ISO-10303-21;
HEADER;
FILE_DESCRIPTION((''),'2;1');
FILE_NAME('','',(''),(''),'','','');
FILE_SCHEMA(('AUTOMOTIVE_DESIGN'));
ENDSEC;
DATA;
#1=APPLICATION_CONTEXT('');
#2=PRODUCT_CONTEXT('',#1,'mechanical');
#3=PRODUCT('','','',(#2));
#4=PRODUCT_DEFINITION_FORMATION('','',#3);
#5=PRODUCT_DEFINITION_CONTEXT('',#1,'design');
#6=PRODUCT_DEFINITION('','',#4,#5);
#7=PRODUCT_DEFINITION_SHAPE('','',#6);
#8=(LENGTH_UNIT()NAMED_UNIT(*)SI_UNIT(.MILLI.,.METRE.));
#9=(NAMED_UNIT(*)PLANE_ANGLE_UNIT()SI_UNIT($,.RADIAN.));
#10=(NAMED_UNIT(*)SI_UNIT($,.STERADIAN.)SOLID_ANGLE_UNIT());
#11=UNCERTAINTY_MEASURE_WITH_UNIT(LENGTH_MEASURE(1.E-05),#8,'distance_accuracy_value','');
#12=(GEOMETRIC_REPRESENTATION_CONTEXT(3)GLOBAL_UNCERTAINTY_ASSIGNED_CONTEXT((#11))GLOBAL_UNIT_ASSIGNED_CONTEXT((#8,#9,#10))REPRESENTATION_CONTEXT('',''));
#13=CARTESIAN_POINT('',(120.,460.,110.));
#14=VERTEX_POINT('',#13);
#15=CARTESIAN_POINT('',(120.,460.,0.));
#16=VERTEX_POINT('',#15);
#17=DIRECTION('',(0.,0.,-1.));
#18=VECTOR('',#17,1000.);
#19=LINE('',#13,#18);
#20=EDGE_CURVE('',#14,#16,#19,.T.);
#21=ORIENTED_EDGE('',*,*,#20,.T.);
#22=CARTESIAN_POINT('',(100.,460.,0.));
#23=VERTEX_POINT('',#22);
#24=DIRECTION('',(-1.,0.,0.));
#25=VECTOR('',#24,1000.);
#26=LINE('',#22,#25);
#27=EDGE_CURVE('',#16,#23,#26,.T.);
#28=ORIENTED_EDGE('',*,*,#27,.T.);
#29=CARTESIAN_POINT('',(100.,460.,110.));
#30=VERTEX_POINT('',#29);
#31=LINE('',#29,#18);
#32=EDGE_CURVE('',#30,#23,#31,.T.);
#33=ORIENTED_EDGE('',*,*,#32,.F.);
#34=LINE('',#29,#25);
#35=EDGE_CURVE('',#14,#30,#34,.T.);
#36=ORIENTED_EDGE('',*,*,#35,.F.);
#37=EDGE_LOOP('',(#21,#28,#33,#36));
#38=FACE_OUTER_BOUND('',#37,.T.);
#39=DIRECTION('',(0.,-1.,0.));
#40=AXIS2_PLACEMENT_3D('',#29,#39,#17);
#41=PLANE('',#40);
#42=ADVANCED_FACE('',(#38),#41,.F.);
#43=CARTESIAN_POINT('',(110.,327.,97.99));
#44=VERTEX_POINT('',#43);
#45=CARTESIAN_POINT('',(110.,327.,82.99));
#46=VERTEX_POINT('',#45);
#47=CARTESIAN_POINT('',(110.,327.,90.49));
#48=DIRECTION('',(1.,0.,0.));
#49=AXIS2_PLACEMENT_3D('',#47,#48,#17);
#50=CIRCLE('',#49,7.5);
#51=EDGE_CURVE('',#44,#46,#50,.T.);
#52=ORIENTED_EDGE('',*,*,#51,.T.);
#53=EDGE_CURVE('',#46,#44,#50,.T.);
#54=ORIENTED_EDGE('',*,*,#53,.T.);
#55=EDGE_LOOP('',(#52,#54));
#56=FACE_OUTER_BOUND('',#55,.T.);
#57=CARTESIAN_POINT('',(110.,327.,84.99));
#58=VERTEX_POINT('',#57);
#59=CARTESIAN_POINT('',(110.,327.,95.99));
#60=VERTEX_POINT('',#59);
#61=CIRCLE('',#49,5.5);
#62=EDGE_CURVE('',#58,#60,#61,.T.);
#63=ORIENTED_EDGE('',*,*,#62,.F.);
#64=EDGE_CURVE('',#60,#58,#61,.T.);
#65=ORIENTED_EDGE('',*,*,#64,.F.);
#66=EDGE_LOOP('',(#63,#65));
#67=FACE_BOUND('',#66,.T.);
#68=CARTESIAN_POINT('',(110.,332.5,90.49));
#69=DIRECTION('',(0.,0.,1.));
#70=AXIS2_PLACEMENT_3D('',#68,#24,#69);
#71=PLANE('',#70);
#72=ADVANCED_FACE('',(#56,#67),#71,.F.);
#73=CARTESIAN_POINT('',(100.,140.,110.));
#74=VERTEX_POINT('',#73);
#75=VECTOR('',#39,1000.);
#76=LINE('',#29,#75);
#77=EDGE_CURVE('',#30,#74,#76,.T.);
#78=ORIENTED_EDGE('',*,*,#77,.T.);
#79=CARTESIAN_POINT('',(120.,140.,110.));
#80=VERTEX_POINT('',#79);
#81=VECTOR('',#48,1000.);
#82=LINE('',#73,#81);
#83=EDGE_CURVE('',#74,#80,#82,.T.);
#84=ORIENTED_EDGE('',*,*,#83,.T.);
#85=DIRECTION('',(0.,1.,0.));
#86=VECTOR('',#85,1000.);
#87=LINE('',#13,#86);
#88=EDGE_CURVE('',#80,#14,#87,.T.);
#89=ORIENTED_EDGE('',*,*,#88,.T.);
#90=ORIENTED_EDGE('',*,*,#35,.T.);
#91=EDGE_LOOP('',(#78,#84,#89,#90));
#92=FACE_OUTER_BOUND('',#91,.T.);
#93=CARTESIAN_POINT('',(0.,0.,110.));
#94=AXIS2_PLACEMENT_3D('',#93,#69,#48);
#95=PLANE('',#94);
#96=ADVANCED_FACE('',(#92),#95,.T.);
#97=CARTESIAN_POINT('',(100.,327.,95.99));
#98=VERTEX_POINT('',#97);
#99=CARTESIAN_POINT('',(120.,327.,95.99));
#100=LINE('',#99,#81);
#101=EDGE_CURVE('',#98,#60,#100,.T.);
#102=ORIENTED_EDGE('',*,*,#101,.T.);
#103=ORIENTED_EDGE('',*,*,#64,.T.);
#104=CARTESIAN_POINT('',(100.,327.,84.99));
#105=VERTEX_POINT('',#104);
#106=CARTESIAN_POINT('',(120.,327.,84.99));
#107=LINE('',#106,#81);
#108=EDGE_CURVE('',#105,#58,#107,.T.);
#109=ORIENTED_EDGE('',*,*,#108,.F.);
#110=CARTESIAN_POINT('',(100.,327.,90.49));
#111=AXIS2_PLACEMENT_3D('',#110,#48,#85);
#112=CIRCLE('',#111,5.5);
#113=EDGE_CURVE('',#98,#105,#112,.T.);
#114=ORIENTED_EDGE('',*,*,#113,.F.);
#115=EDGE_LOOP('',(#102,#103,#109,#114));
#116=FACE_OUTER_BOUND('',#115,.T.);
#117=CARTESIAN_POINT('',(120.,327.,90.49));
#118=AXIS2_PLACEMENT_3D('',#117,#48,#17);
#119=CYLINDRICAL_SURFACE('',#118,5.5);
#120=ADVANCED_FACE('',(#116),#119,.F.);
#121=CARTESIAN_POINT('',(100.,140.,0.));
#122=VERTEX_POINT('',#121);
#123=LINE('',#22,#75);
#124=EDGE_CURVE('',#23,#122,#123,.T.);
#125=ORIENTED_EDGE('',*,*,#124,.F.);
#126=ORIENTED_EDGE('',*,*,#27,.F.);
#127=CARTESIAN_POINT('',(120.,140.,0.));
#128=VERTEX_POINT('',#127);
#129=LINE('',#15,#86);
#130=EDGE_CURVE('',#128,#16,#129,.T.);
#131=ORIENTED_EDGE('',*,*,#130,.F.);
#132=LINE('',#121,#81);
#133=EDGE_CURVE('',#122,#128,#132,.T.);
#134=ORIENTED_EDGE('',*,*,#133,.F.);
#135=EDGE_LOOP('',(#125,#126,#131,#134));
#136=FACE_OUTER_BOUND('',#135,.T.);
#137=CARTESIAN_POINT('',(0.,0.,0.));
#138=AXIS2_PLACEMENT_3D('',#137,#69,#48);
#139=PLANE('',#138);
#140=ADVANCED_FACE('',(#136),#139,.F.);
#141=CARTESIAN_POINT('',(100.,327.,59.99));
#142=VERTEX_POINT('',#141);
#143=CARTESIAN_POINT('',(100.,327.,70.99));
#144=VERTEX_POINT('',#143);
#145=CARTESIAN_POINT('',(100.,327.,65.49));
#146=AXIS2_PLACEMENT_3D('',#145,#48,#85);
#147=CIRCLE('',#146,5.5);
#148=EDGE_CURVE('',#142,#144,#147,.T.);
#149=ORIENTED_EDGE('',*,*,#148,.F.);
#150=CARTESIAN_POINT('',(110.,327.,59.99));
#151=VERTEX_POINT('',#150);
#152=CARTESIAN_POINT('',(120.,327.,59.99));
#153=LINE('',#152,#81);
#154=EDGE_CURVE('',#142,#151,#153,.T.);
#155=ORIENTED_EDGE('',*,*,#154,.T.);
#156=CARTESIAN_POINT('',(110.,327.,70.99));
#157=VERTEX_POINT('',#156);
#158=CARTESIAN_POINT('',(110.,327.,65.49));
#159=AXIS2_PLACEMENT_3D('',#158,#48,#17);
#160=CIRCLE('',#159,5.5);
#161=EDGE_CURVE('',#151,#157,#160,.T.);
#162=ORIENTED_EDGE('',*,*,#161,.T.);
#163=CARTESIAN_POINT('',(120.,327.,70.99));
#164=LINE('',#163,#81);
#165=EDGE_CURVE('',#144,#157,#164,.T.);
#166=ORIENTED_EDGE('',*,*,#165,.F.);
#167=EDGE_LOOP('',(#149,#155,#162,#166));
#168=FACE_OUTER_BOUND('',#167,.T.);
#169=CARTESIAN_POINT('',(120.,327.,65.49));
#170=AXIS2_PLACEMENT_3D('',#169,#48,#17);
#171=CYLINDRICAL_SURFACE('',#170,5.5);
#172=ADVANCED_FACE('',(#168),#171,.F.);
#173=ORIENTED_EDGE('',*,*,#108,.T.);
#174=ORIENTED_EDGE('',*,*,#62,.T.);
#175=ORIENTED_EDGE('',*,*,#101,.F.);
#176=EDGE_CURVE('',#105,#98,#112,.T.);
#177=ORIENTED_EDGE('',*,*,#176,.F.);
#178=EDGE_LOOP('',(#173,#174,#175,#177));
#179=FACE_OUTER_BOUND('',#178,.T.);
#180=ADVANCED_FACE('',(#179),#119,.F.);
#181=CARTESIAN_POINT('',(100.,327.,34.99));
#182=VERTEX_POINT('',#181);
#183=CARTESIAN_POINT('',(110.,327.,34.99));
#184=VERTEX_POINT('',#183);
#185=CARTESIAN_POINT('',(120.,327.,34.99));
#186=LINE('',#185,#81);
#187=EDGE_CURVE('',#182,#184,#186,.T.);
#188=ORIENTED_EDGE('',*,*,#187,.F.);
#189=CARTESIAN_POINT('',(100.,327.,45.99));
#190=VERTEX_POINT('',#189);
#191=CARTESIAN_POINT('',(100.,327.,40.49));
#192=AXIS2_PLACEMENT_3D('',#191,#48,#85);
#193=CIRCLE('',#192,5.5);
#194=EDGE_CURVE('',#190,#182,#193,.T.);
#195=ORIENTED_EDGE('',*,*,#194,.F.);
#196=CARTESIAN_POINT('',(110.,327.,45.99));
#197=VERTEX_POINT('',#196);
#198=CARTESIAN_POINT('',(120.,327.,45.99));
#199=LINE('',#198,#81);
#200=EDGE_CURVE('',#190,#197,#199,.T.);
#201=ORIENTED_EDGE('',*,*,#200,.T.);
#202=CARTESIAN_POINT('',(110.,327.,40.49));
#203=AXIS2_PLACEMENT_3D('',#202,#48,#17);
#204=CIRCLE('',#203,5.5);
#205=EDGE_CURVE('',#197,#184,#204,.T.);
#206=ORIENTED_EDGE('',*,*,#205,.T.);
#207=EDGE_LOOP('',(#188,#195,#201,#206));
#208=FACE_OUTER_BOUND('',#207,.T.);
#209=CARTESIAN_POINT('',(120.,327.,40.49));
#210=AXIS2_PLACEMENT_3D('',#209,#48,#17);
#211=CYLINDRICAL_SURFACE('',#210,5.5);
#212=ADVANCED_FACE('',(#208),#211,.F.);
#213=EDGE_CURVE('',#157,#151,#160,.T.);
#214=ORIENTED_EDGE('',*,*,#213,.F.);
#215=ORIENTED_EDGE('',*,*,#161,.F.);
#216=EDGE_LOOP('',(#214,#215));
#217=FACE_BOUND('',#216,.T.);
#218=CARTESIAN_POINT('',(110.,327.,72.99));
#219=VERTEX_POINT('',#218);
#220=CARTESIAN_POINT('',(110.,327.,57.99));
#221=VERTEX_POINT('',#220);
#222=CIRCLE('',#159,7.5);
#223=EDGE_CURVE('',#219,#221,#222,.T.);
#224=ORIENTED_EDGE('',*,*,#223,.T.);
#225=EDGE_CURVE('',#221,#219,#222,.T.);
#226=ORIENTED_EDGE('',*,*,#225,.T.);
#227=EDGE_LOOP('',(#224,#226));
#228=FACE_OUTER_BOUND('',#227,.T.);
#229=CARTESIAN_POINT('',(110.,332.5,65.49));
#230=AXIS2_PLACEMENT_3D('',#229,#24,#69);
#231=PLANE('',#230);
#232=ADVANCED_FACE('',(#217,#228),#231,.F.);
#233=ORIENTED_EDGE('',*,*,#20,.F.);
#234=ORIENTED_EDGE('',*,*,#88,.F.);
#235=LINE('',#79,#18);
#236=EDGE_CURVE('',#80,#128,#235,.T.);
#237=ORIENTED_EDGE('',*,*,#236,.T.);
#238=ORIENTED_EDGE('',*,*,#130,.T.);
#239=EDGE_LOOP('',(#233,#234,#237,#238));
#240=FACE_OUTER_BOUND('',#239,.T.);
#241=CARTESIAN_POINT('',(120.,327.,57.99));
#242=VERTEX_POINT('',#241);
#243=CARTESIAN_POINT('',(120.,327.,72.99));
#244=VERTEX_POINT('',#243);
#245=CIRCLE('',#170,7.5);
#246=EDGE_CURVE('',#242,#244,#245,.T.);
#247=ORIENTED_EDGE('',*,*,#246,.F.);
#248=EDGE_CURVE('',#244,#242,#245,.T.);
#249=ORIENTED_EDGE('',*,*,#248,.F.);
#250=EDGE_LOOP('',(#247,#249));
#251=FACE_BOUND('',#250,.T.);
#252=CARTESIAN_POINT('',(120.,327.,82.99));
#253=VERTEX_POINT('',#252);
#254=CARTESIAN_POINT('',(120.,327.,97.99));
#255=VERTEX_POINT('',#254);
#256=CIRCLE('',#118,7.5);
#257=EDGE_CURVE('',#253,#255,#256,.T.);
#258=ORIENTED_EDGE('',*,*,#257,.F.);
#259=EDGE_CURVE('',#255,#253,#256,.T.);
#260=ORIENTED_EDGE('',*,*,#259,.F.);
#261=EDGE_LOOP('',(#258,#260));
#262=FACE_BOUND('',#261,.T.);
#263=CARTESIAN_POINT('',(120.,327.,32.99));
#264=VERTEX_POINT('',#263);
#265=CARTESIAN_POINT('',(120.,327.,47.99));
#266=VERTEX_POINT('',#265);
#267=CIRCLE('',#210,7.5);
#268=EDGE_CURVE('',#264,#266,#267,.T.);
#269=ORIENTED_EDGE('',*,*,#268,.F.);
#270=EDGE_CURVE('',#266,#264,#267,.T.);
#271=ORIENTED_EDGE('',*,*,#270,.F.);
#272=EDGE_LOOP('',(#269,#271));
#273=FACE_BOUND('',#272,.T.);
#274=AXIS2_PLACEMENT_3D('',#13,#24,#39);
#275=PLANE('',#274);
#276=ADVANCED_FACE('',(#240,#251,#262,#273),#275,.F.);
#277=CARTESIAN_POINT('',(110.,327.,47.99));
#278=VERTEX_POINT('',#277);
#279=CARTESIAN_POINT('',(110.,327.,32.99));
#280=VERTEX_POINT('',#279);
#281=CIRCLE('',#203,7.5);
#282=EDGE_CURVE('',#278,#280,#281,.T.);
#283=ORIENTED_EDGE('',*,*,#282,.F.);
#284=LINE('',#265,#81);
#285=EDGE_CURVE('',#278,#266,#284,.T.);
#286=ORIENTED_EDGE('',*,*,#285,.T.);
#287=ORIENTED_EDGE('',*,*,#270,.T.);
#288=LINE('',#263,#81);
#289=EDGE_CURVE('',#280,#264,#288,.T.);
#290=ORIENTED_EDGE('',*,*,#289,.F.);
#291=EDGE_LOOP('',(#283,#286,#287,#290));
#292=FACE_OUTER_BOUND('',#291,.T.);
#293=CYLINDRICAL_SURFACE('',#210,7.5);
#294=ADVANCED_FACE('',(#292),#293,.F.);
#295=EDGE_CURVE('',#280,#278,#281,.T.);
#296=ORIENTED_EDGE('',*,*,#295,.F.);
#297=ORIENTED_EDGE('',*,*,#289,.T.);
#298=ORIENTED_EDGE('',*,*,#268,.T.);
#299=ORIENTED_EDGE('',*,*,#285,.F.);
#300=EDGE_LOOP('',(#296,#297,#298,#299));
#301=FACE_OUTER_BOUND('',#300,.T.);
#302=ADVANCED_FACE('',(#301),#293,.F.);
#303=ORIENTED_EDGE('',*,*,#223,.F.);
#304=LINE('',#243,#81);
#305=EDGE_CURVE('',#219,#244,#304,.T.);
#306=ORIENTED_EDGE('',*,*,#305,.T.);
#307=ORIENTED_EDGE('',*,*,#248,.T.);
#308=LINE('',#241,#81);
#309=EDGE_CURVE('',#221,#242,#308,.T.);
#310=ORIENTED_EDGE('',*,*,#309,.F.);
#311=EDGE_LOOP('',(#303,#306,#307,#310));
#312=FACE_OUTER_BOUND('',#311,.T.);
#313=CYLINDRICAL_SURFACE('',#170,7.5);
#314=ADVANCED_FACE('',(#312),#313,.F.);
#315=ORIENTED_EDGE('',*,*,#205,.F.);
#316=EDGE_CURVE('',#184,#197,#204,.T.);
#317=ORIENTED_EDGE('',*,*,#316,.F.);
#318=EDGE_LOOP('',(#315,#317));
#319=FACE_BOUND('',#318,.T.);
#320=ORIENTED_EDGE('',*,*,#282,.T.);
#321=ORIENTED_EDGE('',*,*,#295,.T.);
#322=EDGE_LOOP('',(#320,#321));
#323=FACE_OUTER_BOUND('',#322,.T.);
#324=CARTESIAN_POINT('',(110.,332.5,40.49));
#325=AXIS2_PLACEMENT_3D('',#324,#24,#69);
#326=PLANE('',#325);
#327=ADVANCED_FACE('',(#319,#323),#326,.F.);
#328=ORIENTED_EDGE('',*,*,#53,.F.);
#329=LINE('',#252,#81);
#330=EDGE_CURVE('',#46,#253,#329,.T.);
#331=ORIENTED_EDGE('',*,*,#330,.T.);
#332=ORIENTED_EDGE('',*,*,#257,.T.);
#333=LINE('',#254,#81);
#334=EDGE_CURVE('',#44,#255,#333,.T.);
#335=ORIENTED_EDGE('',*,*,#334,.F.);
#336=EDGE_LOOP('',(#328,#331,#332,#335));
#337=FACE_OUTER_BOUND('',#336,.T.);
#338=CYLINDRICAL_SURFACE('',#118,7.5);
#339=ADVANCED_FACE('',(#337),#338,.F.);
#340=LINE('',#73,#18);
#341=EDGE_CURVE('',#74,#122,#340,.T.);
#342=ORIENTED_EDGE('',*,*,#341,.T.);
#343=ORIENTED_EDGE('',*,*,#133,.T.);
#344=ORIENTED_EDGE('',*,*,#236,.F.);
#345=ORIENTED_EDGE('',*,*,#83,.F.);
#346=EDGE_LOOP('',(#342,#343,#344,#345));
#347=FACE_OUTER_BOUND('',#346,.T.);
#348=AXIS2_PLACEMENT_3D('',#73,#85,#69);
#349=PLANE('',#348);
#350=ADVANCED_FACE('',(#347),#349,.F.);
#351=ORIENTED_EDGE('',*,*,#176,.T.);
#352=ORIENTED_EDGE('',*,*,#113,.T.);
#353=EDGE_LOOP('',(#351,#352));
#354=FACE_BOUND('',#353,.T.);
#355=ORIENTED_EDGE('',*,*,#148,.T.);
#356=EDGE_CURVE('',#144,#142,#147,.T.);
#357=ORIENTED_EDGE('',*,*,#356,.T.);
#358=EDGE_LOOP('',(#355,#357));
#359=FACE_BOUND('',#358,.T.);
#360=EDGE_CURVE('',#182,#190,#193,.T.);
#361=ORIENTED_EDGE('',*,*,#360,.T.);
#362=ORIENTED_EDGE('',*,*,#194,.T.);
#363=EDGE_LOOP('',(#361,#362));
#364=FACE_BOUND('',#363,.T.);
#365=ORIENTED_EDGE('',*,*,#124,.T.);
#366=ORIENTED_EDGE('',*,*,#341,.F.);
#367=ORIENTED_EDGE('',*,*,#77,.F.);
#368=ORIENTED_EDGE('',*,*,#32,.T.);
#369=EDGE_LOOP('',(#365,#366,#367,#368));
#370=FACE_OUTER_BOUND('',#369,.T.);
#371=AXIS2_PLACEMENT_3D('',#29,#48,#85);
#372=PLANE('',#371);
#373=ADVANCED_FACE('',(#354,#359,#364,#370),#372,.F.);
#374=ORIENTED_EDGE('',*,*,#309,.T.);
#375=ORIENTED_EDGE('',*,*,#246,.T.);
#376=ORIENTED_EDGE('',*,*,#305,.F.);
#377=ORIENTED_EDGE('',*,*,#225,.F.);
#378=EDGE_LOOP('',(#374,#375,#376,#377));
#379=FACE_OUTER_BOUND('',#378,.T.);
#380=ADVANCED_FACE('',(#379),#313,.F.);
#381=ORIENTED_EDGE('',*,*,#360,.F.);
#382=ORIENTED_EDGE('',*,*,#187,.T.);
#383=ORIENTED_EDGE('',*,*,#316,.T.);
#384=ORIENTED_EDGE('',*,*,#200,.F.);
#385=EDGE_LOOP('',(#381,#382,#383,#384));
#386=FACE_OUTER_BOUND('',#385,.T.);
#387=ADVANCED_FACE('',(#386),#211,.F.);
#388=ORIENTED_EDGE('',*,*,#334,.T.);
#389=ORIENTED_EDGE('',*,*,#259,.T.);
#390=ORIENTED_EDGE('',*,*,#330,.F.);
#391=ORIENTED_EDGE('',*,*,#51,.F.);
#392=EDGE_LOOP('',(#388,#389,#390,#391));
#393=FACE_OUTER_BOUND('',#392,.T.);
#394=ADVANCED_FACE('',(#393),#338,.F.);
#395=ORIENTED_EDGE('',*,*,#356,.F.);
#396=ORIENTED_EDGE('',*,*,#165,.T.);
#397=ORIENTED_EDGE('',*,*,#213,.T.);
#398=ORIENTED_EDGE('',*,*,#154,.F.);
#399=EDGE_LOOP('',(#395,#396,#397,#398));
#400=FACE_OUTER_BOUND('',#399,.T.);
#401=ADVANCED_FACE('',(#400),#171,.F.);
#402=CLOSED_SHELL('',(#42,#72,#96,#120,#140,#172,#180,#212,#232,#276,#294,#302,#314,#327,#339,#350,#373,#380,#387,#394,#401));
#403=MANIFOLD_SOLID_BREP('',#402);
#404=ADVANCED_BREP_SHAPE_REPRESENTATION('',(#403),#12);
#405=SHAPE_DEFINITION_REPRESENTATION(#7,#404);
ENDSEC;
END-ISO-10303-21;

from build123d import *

# Parameters (mm, degrees)
SKETCH1_W                                = 20
SKETCH1_H                                = 320
BOSS_EXTRUDE1_DEPTH                      = 110
CBORE_FOR_M10_HEX_HEAD_BOLT1_D           = 11
CBORE_FOR_M10_HEX_HEAD_BOLT1_DEPTH       = 22.25
CBORE_FOR_M10_HEX_HEAD_BOLT1_CBORE_D     = 15
CBORE_FOR_M10_HEX_HEAD_BOLT1_CBORE_DEPTH = 10
CBORE_FOR_M10_HEX_HEAD_BOLT1_TIP         = 3.304733405


with BuildPart() as part:
    # Sketch1 → Boss-Extrude1 (new body)
    with BuildSketch(Plane.XY):
        with Locations((110, 300)):
            Rectangle(SKETCH1_W, SKETCH1_H)
    extrude(amount=BOSS_EXTRUDE1_DEPTH)

    # CBORE for M10 Hex Head Bolt1
    with Locations(Plane(origin=(120, 0, 0), x_dir=(0, 0, -1), z_dir=(1, 0, 0))):
        with Locations((-90.49, 327), (-65.49, 327), (-40.49, 327)):
            CounterBoreHole(CBORE_FOR_M10_HEX_HEAD_BOLT1_D / 2, CBORE_FOR_M10_HEX_HEAD_BOLT1_CBORE_D / 2, CBORE_FOR_M10_HEX_HEAD_BOLT1_CBORE_DEPTH, depth=CBORE_FOR_M10_HEX_HEAD_BOLT1_DEPTH)
            with Locations((0, 0, -(CBORE_FOR_M10_HEX_HEAD_BOLT1_DEPTH + CBORE_FOR_M10_HEX_HEAD_BOLT1_TIP / 2))):  # 118° drill point
                Cone(0, CBORE_FOR_M10_HEX_HEAD_BOLT1_D / 2, CBORE_FOR_M10_HEX_HEAD_BOLT1_TIP, mode=Mode.SUBTRACT)


solid = part.part
